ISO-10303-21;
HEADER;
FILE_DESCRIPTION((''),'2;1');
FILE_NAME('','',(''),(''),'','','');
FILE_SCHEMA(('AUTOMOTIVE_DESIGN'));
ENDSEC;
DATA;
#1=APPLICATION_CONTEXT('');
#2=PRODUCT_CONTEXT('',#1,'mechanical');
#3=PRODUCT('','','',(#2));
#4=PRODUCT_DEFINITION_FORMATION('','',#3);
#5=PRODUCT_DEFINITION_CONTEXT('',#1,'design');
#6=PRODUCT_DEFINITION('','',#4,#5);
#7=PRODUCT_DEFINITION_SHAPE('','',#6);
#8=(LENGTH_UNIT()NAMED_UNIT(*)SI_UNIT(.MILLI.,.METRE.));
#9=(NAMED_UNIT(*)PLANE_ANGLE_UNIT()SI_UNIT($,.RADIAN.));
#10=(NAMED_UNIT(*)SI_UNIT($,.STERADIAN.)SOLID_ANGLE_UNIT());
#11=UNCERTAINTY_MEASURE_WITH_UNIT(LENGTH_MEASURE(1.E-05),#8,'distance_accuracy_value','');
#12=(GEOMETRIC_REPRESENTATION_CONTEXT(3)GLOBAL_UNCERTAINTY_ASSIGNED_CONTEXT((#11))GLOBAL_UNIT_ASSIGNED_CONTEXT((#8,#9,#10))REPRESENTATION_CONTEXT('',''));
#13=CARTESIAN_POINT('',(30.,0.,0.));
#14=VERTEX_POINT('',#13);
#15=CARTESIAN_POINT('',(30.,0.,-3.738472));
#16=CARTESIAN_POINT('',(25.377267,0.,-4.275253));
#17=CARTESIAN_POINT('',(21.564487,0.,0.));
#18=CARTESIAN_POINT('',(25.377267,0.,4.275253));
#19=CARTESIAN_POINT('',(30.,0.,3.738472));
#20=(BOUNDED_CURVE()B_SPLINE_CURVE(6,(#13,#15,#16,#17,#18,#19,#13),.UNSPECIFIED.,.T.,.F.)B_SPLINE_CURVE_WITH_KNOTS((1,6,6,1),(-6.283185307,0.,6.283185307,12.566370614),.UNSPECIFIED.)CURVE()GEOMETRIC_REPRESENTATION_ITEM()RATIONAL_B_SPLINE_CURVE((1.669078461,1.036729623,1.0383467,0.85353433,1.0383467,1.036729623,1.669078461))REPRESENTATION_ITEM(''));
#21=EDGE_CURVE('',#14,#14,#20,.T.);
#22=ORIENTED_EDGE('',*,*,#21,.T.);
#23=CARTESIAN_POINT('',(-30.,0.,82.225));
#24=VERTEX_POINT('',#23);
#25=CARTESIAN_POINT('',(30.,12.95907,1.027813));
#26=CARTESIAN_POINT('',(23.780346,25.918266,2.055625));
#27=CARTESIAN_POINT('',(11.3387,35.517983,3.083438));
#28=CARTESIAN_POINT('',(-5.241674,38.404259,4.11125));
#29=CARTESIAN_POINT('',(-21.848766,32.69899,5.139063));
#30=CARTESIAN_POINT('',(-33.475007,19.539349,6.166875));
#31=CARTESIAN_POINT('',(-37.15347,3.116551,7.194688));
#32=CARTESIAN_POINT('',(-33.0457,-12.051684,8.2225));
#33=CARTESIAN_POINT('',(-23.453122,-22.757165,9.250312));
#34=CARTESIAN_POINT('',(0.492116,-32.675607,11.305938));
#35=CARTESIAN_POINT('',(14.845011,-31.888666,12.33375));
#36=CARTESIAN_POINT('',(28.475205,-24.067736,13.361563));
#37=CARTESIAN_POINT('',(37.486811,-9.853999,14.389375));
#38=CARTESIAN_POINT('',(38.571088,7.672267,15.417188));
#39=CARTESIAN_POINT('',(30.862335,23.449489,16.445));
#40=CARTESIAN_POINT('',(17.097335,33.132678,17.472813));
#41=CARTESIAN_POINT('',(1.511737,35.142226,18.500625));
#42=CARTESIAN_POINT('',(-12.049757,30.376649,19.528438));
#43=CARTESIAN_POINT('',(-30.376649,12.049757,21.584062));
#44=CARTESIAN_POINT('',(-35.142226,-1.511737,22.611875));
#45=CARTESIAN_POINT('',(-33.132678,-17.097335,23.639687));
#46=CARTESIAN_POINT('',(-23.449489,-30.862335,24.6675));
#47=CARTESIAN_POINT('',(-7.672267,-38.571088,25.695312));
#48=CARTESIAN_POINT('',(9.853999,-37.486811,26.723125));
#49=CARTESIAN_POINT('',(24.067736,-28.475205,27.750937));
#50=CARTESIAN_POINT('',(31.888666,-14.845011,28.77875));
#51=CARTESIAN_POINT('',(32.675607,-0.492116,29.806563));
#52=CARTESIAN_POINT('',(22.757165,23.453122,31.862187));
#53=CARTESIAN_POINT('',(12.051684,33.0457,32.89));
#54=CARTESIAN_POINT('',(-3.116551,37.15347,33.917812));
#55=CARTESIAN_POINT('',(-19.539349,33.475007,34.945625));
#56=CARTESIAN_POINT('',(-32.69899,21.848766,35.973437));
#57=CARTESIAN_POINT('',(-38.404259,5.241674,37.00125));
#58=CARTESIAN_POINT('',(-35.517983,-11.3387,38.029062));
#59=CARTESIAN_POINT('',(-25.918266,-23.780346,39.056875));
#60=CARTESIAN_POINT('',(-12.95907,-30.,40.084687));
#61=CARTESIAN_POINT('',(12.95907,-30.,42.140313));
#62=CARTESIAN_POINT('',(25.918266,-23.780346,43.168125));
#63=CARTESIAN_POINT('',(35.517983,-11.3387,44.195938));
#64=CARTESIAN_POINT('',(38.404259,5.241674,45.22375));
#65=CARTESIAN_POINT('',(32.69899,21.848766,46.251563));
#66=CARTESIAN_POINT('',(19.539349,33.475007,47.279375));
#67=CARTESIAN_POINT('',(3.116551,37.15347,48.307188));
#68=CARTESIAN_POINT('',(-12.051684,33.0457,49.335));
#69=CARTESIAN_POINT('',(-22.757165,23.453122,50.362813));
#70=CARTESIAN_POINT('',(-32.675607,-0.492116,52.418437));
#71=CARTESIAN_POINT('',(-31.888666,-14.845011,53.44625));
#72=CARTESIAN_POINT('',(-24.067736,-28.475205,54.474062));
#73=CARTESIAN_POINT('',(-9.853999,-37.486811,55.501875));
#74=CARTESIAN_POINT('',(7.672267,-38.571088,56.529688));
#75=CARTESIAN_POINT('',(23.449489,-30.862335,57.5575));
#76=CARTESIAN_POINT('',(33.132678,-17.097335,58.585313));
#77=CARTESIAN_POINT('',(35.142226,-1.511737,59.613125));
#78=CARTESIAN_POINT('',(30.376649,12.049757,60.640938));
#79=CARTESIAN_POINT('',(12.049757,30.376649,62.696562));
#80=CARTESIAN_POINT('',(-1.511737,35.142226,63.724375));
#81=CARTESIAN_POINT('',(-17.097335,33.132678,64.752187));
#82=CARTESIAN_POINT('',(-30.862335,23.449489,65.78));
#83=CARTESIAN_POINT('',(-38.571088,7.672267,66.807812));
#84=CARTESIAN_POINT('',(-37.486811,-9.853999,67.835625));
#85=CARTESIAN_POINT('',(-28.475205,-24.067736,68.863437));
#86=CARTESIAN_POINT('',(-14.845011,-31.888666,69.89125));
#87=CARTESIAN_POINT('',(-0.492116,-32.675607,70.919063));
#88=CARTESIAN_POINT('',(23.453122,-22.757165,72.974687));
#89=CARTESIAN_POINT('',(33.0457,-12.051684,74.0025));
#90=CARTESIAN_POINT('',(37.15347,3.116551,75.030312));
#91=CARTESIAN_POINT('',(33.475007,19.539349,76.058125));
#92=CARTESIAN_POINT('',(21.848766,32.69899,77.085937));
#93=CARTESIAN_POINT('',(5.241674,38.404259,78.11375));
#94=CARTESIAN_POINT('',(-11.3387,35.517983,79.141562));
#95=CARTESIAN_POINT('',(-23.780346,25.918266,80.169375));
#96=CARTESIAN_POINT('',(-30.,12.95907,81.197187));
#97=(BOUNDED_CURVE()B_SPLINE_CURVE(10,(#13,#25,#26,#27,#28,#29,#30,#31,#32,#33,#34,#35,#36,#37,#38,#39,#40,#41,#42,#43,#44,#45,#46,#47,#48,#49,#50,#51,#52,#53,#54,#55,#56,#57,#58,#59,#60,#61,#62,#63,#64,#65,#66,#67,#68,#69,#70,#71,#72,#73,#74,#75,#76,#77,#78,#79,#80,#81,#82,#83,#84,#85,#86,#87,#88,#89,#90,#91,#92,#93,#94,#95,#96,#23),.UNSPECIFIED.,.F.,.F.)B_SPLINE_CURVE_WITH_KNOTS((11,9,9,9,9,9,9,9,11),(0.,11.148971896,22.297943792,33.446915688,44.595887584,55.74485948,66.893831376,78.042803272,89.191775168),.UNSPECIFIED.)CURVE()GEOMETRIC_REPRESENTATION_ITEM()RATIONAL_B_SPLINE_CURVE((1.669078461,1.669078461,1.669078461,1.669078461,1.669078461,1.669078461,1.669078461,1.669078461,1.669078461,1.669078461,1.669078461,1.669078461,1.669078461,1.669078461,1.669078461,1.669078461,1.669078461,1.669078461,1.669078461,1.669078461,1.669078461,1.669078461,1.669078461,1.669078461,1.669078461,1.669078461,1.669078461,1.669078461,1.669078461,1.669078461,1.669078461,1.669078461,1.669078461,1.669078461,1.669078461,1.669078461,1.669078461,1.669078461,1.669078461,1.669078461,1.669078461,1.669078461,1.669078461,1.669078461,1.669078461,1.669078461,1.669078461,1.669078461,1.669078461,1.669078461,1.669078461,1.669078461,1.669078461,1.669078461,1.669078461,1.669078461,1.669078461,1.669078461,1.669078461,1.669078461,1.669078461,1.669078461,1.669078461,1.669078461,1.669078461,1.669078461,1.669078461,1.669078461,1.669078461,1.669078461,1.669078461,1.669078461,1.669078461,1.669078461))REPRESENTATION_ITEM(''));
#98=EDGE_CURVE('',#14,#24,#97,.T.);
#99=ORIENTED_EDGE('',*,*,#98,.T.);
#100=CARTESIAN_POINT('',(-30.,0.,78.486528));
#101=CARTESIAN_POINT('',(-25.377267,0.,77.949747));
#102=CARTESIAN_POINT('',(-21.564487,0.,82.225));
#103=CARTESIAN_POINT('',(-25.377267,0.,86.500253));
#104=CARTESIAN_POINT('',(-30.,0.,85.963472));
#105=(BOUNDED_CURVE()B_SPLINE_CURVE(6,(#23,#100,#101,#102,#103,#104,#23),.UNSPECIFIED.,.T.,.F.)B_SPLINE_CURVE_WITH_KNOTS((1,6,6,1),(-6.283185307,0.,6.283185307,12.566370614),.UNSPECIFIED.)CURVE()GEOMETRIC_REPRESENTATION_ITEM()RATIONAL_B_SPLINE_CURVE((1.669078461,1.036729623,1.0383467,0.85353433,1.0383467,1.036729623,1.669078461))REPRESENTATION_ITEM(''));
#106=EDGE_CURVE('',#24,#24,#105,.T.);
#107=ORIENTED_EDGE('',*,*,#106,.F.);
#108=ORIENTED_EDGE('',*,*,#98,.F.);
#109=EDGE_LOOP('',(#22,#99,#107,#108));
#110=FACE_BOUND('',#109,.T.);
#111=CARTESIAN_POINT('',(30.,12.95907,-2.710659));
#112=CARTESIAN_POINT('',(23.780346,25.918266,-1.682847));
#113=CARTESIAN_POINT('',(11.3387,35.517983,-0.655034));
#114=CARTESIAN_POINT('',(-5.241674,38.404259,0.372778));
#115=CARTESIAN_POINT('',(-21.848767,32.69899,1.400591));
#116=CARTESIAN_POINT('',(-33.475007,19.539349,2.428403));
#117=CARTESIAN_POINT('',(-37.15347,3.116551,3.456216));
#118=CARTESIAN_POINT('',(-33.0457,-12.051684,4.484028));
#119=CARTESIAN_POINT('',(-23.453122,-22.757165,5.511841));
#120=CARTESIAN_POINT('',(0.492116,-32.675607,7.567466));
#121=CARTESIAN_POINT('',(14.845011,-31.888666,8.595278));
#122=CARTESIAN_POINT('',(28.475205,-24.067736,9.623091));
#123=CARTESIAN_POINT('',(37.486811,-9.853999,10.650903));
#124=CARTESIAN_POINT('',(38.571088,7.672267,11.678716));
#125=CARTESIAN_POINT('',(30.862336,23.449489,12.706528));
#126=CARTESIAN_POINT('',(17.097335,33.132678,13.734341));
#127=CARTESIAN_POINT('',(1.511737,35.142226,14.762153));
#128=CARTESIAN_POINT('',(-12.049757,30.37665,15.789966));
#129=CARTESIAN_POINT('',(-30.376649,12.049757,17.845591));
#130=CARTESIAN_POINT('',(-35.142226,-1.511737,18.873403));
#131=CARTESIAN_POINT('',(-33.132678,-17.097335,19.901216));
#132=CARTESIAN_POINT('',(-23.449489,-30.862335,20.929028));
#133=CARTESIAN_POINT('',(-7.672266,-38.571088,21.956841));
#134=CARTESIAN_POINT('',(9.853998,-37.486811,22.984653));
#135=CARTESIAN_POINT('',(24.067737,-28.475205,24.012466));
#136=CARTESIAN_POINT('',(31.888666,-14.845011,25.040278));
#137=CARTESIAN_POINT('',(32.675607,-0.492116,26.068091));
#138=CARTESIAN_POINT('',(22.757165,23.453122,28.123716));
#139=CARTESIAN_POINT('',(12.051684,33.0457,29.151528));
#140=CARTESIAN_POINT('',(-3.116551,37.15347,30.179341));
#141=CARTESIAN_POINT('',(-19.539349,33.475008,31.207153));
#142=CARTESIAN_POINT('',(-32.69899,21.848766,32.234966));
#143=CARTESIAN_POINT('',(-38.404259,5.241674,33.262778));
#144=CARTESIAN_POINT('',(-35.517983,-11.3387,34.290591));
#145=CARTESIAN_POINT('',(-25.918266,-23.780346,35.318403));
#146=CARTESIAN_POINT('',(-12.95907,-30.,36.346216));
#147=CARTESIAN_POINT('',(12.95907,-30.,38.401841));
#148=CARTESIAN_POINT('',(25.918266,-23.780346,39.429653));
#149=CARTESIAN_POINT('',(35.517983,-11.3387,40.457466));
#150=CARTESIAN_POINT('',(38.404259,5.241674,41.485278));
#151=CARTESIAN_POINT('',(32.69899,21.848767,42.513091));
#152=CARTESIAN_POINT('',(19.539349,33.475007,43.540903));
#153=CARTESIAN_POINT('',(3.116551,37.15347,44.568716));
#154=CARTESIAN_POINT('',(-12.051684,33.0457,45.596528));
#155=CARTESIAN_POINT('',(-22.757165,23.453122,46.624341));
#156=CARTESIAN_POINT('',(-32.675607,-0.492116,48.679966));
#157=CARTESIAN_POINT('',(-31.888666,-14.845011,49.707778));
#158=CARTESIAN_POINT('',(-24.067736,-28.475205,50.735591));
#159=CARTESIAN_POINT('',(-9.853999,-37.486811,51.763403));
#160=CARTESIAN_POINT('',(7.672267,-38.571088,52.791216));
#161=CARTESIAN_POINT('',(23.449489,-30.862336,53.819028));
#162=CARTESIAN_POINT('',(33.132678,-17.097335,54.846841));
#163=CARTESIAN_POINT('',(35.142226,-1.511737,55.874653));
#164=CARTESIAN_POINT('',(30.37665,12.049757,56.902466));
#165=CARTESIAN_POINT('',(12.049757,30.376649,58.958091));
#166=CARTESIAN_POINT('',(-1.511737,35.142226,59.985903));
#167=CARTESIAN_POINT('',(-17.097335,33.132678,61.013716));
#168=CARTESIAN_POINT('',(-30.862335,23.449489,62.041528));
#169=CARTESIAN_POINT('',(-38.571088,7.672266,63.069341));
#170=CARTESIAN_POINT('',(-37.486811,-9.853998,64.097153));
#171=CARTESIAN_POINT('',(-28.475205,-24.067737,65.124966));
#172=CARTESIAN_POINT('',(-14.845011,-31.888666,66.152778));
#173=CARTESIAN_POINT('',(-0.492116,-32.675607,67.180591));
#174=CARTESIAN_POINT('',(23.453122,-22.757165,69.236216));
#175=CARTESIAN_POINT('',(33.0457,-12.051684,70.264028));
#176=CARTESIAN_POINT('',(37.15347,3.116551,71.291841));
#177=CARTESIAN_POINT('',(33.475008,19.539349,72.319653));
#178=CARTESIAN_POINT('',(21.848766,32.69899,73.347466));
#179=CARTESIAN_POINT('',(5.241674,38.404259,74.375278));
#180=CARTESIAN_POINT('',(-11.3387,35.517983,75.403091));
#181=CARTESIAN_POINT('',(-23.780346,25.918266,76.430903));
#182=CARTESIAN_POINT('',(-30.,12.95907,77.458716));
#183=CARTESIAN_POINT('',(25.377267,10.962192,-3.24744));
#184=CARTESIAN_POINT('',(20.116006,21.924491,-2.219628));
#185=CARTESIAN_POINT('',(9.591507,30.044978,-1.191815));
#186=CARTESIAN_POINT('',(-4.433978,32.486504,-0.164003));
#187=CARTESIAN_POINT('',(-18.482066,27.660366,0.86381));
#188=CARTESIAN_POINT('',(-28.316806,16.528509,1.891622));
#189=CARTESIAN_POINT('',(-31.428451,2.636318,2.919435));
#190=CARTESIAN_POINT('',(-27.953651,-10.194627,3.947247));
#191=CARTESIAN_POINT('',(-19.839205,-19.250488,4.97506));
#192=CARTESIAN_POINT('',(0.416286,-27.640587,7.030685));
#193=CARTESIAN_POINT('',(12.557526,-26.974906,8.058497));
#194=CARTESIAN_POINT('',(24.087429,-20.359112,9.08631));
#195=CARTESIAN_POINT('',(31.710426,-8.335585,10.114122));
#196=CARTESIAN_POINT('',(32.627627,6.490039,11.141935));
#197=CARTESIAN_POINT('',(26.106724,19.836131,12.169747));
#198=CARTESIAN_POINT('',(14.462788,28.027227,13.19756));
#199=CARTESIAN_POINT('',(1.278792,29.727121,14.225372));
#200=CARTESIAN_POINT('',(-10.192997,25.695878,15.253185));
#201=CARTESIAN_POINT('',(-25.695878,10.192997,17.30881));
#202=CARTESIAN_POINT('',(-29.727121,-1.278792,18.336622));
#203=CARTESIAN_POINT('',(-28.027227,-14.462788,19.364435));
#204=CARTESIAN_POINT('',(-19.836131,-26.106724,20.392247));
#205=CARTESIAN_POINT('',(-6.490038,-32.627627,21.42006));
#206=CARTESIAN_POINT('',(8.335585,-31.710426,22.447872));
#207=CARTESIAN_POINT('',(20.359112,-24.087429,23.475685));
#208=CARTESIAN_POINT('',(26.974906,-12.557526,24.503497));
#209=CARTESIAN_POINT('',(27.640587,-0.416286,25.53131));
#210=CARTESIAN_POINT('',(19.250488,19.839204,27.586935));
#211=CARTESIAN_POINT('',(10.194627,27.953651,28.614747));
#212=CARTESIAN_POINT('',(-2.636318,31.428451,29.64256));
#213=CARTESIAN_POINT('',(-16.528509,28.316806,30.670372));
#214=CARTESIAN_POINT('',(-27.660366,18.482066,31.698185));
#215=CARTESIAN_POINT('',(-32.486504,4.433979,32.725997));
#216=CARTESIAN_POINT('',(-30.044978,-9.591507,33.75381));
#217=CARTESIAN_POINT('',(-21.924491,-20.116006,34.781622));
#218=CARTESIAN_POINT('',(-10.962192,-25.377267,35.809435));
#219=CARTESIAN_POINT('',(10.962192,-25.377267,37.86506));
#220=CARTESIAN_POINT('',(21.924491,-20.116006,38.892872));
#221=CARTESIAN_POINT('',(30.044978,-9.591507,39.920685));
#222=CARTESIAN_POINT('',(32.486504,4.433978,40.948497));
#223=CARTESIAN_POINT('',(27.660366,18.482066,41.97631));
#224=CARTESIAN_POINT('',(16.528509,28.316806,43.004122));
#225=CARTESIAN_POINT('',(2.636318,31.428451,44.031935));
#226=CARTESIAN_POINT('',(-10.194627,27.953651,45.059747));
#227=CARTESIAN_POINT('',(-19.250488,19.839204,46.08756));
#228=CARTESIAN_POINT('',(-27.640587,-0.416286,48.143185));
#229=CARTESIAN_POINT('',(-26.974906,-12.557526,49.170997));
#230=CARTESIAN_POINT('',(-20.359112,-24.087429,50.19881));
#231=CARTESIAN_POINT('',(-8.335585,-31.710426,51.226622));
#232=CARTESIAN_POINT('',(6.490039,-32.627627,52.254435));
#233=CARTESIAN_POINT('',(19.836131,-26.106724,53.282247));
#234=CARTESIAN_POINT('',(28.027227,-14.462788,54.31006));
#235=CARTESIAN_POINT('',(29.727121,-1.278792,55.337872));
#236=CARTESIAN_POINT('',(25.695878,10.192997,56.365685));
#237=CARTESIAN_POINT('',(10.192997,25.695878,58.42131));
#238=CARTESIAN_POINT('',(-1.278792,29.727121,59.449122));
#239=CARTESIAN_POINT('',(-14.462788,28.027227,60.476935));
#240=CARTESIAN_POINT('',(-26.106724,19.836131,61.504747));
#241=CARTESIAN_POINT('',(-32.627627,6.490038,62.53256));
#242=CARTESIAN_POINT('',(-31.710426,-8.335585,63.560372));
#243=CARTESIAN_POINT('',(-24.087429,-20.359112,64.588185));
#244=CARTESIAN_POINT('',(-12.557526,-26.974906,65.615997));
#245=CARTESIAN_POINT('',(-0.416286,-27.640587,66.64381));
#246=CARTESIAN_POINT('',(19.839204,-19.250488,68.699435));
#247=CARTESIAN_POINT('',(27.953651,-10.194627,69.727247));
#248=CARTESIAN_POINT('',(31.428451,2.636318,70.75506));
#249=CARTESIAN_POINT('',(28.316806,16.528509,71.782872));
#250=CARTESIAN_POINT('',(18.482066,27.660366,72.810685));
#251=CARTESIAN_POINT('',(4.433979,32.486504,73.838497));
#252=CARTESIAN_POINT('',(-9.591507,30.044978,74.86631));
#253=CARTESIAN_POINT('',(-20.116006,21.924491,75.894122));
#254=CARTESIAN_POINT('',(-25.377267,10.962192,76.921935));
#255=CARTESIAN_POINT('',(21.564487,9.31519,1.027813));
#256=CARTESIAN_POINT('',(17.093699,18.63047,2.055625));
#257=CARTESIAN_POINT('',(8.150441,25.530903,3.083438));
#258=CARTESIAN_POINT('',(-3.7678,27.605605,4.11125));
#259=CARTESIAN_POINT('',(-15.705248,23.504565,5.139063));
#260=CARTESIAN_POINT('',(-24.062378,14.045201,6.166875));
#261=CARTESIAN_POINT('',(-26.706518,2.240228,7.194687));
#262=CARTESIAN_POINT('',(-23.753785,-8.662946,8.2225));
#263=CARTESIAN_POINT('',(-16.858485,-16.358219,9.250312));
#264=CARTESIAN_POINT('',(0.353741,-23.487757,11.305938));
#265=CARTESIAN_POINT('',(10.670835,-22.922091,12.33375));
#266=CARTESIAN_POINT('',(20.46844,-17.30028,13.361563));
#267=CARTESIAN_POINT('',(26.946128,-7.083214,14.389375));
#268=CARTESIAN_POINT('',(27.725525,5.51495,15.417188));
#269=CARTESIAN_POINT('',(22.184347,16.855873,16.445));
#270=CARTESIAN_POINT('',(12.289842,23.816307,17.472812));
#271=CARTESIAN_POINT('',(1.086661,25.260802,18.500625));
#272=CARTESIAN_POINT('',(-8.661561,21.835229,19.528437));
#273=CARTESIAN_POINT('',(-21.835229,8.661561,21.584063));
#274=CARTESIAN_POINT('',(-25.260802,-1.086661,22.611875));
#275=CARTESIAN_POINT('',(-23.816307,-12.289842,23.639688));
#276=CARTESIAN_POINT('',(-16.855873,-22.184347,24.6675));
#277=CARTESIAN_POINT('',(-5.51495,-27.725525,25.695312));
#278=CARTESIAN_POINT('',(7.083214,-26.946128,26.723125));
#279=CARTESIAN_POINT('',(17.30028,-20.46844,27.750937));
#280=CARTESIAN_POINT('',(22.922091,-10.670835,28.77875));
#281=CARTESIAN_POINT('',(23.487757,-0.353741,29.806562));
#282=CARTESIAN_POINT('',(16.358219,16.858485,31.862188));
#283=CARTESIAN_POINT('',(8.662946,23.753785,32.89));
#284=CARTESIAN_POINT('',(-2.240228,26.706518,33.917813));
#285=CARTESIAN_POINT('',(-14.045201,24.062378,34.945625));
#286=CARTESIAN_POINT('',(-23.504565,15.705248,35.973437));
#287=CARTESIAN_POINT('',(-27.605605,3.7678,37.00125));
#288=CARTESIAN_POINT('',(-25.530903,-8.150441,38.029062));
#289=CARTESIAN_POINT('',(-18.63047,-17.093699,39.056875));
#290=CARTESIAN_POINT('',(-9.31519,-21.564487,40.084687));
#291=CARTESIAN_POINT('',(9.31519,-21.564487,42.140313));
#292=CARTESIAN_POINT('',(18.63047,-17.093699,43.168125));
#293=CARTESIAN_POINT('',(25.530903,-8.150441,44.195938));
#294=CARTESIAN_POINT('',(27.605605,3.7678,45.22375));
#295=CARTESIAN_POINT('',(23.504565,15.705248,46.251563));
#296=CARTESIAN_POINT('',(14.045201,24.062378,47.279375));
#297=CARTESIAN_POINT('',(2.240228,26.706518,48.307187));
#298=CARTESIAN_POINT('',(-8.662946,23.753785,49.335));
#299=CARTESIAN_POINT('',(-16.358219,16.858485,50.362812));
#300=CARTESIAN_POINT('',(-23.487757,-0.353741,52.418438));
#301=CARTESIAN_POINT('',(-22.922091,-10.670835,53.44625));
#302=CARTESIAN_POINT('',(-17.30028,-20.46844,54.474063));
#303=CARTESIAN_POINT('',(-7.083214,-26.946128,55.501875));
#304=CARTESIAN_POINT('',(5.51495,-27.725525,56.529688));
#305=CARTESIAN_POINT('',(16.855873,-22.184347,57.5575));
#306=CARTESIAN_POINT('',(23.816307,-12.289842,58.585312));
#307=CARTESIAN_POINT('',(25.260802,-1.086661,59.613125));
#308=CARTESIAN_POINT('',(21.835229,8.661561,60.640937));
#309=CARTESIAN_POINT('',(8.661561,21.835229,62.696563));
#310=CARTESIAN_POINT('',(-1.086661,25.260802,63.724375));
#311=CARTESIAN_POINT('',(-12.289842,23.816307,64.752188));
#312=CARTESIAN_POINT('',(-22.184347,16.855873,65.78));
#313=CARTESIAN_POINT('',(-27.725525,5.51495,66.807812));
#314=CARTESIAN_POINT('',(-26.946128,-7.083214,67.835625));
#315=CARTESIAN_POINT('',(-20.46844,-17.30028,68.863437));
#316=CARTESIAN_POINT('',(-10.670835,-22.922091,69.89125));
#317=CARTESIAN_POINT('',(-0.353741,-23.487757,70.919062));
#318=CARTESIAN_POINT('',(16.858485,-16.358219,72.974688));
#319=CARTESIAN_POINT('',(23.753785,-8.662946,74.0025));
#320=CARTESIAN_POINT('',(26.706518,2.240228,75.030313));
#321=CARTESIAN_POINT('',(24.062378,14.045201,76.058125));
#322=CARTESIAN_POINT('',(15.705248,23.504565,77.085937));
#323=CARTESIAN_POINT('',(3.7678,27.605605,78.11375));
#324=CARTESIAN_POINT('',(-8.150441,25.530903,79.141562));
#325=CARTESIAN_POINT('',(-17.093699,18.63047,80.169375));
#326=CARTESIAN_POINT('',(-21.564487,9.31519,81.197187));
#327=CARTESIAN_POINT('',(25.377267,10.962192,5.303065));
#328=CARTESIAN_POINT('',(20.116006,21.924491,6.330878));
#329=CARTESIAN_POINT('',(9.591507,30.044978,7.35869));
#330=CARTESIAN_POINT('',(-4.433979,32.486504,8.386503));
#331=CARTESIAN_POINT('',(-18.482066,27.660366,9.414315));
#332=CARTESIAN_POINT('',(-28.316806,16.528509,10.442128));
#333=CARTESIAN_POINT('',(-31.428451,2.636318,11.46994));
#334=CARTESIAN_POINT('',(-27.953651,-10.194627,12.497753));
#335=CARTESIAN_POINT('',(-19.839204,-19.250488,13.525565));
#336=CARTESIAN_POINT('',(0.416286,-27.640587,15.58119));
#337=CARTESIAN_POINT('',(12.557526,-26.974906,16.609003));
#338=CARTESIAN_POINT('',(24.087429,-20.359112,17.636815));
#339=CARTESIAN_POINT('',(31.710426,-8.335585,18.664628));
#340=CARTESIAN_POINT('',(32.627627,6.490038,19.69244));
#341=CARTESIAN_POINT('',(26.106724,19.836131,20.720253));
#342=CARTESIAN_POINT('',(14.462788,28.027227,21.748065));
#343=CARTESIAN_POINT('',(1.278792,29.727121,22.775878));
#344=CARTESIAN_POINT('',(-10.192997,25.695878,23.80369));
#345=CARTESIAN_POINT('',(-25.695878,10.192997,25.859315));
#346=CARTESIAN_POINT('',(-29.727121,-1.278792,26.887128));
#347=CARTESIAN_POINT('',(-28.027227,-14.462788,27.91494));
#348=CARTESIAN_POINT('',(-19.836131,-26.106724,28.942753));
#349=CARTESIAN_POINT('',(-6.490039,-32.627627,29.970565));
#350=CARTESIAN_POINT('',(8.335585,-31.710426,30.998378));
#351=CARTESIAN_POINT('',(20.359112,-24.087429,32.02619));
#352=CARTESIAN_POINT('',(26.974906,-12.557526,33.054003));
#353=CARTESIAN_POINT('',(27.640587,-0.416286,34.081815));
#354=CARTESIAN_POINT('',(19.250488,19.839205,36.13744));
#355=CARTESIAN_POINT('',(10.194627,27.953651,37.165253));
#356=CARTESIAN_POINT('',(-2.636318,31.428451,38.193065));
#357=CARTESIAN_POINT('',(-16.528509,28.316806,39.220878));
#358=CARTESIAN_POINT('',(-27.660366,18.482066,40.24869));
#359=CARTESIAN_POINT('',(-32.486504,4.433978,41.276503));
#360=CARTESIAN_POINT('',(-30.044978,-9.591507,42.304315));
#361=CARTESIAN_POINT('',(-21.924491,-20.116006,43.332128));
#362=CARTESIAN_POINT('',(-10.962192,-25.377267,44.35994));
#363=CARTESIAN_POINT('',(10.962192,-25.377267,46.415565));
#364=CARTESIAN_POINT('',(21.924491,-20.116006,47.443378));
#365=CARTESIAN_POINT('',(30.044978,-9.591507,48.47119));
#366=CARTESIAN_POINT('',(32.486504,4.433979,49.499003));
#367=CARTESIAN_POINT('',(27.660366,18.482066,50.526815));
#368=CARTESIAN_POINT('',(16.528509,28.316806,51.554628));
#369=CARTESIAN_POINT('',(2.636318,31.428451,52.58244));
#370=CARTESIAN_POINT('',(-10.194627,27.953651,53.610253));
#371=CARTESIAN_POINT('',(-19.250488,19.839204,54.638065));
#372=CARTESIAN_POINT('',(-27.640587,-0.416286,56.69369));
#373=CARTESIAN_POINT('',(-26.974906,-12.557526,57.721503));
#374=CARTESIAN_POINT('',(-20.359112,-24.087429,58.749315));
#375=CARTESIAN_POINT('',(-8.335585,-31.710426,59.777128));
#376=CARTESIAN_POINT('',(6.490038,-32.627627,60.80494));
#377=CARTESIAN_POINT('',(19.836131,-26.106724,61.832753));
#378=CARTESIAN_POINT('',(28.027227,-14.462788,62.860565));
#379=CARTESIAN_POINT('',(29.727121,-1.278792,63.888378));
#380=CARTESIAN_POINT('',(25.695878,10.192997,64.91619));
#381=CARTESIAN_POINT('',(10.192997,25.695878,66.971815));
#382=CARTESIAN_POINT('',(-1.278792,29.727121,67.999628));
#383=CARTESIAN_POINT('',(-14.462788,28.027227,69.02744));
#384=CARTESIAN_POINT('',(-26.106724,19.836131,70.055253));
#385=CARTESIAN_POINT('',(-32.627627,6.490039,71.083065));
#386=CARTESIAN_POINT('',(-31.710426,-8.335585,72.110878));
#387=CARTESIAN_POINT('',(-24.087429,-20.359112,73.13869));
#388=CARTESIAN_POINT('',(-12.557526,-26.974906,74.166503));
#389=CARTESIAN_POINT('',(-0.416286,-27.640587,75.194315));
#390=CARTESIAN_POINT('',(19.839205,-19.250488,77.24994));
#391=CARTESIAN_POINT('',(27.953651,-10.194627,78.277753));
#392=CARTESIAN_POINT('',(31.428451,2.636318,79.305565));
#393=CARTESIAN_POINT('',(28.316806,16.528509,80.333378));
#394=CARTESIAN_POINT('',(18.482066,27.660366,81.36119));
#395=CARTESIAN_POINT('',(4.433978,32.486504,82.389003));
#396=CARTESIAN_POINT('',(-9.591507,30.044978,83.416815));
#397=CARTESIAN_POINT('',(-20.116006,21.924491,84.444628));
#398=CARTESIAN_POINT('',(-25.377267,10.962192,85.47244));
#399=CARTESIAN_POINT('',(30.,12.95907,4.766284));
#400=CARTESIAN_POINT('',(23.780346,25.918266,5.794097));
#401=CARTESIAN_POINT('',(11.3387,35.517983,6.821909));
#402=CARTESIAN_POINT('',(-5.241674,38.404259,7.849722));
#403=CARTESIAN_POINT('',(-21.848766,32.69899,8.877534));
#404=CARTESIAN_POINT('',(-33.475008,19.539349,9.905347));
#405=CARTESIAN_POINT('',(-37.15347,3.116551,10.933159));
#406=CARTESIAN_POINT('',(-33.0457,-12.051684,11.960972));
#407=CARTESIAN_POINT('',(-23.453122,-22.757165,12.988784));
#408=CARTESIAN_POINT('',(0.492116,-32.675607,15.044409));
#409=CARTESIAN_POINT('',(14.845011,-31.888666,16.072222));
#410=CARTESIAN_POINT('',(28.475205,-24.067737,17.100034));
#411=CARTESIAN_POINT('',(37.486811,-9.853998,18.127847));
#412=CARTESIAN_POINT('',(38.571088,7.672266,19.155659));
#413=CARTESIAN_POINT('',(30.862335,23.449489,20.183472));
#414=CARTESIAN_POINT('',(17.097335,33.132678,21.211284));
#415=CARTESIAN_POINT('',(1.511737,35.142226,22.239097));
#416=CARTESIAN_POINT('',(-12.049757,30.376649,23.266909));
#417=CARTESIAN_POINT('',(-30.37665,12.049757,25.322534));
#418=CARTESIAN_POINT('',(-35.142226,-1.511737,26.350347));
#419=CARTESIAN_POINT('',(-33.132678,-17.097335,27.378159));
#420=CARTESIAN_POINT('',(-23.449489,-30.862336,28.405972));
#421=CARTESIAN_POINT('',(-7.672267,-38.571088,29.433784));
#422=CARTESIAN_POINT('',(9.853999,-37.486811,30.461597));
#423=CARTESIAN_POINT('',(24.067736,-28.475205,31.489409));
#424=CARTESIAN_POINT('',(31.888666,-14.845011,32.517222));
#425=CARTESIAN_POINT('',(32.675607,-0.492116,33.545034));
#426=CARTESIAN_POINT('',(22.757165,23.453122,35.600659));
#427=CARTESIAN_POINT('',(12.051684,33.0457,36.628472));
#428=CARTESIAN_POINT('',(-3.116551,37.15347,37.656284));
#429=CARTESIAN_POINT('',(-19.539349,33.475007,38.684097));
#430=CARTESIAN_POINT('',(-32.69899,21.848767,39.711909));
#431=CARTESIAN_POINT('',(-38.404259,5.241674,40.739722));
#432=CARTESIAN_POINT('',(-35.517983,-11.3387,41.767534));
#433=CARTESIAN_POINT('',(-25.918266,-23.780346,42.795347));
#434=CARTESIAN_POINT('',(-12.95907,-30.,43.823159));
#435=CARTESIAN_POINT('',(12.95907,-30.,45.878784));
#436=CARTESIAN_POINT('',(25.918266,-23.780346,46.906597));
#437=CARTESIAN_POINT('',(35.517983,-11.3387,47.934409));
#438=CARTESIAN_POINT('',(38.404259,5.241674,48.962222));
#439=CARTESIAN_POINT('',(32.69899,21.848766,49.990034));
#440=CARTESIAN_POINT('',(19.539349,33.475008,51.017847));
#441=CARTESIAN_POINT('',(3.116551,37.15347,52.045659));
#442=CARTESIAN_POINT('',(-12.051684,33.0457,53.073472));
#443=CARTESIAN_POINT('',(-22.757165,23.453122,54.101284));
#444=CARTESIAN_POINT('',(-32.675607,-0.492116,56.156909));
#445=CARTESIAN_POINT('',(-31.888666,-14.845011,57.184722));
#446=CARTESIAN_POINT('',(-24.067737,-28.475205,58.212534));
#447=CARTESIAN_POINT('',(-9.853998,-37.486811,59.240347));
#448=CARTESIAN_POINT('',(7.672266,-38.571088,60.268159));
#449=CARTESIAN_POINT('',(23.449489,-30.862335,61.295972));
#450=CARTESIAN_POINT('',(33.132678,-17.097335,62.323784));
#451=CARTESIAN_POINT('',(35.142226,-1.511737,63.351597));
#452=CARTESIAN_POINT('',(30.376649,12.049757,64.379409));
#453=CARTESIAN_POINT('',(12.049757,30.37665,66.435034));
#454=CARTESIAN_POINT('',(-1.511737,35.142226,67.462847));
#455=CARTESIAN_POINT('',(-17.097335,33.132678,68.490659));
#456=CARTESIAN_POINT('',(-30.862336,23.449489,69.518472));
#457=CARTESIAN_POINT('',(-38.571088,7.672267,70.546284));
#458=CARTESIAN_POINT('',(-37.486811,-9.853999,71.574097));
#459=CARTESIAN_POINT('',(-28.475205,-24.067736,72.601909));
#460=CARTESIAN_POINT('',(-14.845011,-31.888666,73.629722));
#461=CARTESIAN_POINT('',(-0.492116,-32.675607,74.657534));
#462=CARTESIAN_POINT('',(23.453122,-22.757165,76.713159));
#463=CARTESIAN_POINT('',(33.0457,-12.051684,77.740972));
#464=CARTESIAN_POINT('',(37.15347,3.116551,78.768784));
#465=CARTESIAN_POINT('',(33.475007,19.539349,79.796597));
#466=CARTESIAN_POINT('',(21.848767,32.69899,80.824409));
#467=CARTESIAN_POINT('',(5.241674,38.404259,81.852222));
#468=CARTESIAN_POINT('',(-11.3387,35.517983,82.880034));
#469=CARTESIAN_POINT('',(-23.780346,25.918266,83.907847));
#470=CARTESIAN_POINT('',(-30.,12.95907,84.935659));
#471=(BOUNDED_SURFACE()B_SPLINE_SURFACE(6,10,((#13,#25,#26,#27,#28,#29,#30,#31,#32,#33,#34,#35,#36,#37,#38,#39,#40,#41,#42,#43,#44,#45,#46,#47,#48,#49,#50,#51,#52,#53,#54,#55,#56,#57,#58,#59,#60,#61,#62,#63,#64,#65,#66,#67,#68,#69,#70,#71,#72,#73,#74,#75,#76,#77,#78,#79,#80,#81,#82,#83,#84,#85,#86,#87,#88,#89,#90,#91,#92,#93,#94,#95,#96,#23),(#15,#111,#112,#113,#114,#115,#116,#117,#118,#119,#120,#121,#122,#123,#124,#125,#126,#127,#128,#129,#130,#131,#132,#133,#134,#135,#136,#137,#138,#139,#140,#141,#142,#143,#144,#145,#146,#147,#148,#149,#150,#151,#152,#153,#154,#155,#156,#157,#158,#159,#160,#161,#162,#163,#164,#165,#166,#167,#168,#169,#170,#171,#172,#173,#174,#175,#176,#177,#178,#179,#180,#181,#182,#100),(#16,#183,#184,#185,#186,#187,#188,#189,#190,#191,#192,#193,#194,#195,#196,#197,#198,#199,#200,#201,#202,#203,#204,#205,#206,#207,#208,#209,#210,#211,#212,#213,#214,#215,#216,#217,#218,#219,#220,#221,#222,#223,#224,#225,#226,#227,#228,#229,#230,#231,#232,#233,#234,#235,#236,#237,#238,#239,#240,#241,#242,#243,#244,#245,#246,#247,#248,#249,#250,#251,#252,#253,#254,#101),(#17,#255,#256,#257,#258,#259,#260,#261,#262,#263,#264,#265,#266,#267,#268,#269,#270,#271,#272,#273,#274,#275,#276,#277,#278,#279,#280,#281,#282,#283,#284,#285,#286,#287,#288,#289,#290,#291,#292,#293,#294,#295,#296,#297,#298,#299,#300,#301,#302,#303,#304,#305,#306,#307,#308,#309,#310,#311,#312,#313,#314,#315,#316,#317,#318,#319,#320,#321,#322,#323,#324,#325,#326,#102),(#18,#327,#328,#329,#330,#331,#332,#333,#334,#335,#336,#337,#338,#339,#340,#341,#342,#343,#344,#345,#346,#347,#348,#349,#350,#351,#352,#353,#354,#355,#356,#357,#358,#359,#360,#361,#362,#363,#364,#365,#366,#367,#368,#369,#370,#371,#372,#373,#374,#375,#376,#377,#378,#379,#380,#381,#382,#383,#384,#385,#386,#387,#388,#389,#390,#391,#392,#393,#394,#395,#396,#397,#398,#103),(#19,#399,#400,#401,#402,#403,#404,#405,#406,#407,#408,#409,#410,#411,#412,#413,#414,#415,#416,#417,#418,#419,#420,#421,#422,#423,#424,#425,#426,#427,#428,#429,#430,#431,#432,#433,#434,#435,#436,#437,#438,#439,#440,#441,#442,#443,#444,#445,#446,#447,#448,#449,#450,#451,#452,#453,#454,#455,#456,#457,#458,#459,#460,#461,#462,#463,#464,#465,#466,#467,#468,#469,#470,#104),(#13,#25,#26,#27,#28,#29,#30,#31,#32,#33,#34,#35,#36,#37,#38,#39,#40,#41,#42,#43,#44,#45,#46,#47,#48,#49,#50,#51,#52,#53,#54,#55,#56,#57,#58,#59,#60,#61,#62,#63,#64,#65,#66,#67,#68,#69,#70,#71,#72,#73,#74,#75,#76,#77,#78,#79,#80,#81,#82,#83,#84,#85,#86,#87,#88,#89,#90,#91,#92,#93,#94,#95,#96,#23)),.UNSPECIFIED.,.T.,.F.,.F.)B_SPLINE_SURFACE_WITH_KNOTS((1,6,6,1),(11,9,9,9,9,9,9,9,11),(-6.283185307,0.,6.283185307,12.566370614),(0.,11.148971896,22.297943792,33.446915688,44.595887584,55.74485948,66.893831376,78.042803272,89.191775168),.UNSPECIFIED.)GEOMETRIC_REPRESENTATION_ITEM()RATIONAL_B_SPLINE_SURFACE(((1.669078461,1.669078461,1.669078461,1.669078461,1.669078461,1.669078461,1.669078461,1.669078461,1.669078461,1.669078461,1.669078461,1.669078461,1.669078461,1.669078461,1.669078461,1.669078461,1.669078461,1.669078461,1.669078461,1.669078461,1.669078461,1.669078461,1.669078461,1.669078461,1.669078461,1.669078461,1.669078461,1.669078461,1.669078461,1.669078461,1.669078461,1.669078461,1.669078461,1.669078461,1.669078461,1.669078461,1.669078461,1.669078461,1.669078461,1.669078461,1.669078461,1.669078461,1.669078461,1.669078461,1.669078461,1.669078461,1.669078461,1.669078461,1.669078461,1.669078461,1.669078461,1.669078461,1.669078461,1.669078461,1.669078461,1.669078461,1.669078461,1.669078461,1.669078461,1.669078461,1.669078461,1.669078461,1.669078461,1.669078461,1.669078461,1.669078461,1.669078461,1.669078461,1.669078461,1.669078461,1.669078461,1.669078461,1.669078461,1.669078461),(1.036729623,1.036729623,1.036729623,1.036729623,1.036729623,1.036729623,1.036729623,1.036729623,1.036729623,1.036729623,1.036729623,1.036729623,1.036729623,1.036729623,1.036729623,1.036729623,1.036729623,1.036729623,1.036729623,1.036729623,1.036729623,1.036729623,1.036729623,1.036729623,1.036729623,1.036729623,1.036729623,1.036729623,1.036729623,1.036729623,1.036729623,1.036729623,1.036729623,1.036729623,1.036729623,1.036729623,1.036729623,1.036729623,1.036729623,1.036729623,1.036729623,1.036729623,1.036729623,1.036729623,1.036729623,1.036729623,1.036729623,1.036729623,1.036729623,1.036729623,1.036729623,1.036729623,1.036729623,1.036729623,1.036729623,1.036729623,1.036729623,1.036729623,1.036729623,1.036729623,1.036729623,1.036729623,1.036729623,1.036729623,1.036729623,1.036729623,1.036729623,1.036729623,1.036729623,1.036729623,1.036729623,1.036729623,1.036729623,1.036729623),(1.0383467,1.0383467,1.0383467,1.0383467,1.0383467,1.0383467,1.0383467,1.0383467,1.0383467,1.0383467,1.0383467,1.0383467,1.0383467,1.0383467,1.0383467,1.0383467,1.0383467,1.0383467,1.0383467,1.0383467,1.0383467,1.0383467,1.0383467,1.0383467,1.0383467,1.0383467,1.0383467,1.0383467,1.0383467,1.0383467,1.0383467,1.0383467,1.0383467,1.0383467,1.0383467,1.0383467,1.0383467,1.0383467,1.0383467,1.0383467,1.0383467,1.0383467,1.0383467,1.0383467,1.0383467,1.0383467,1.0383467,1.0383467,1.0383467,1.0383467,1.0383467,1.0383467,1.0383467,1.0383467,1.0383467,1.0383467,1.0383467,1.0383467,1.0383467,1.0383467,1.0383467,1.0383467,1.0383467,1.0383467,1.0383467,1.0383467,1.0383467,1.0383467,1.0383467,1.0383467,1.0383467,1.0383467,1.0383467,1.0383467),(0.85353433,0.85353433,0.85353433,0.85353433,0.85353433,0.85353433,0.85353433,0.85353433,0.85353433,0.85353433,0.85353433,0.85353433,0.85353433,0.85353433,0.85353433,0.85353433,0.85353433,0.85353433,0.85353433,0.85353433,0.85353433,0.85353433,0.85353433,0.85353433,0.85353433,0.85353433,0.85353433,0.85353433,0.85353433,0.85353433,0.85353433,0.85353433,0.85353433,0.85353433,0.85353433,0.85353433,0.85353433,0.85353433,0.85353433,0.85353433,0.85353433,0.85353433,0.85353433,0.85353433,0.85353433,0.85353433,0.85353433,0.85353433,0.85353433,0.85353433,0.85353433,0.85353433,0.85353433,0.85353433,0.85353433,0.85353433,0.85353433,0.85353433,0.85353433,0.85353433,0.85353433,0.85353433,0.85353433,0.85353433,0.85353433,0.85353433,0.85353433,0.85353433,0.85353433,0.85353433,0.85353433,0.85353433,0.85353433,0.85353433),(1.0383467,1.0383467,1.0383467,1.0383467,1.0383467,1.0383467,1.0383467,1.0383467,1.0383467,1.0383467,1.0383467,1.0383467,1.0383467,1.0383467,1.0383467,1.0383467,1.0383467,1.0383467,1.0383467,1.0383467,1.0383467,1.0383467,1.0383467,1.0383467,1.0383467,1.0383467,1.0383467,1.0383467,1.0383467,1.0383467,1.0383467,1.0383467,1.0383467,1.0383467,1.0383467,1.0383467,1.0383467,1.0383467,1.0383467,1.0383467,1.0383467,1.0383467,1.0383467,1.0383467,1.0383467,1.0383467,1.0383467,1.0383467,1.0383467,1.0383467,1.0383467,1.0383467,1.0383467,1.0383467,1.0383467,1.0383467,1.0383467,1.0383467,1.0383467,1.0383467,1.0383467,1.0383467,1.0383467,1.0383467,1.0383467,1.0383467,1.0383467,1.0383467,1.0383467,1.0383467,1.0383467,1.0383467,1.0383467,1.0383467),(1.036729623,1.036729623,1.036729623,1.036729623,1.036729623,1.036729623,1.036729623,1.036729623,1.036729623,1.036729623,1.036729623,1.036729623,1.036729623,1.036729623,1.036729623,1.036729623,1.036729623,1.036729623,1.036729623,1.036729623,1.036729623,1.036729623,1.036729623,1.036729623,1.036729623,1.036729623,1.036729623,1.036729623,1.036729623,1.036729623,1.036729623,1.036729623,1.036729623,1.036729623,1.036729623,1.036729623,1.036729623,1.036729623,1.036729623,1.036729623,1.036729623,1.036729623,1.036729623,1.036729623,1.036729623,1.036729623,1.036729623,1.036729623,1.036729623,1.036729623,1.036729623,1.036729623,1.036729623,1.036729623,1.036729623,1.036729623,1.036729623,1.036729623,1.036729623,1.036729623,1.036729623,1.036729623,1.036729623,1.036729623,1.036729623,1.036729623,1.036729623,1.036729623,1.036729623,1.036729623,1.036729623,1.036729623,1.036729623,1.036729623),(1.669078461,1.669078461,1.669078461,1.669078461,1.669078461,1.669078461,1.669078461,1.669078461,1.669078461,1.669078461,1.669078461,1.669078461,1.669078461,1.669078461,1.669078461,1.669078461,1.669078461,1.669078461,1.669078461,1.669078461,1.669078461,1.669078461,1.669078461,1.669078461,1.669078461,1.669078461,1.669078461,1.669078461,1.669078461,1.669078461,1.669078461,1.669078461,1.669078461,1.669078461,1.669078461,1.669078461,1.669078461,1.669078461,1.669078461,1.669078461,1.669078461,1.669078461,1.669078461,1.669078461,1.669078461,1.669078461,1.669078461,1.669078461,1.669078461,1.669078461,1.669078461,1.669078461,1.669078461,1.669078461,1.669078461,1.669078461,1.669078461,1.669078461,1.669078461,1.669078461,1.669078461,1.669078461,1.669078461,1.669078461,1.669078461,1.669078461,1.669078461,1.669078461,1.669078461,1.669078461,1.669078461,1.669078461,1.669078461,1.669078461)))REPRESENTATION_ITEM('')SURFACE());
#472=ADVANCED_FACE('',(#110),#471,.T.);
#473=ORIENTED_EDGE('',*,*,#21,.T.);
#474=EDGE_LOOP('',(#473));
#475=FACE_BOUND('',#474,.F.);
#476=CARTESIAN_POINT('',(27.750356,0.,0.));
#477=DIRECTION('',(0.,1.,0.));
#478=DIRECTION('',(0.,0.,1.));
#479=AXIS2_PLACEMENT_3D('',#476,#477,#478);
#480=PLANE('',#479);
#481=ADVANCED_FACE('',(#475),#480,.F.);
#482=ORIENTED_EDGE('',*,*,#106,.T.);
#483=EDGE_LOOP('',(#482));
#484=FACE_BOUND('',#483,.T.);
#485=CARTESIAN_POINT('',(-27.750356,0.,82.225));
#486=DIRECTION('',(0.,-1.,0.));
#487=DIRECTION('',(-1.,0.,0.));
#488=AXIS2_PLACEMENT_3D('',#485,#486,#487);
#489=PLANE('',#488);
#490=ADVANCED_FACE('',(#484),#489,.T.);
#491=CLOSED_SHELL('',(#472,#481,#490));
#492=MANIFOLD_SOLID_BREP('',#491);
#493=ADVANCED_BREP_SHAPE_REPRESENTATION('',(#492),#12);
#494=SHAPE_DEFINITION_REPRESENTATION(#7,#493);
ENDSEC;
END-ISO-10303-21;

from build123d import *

# Parameters (mm, degrees)
SWEEP1_PITCH  = 14.95
SWEEP1_HEIGHT = 82.225
SWEEP1_RADIUS = 30
SKETCH2_R     = 2.25


with BuildPart() as part:
    # Sweep1: sweep along a helix
    with BuildLine() as sweep1_path:
        Helix(SWEEP1_PITCH, SWEEP1_HEIGHT, SWEEP1_RADIUS, center=(0, 0, 0), direction=(0, 0, 1))
    # Sketch2 → Sweep1 (sweep)
    with BuildSketch(Plane(origin=(0, 0, 0), x_dir=(1, 0, 0), z_dir=(0, 1, 0))):
        with Locations((27.75, 0)):
            Circle(SKETCH2_R)
    sweep(path=sweep1_path.line, is_frenet=True)


solid = part.part
